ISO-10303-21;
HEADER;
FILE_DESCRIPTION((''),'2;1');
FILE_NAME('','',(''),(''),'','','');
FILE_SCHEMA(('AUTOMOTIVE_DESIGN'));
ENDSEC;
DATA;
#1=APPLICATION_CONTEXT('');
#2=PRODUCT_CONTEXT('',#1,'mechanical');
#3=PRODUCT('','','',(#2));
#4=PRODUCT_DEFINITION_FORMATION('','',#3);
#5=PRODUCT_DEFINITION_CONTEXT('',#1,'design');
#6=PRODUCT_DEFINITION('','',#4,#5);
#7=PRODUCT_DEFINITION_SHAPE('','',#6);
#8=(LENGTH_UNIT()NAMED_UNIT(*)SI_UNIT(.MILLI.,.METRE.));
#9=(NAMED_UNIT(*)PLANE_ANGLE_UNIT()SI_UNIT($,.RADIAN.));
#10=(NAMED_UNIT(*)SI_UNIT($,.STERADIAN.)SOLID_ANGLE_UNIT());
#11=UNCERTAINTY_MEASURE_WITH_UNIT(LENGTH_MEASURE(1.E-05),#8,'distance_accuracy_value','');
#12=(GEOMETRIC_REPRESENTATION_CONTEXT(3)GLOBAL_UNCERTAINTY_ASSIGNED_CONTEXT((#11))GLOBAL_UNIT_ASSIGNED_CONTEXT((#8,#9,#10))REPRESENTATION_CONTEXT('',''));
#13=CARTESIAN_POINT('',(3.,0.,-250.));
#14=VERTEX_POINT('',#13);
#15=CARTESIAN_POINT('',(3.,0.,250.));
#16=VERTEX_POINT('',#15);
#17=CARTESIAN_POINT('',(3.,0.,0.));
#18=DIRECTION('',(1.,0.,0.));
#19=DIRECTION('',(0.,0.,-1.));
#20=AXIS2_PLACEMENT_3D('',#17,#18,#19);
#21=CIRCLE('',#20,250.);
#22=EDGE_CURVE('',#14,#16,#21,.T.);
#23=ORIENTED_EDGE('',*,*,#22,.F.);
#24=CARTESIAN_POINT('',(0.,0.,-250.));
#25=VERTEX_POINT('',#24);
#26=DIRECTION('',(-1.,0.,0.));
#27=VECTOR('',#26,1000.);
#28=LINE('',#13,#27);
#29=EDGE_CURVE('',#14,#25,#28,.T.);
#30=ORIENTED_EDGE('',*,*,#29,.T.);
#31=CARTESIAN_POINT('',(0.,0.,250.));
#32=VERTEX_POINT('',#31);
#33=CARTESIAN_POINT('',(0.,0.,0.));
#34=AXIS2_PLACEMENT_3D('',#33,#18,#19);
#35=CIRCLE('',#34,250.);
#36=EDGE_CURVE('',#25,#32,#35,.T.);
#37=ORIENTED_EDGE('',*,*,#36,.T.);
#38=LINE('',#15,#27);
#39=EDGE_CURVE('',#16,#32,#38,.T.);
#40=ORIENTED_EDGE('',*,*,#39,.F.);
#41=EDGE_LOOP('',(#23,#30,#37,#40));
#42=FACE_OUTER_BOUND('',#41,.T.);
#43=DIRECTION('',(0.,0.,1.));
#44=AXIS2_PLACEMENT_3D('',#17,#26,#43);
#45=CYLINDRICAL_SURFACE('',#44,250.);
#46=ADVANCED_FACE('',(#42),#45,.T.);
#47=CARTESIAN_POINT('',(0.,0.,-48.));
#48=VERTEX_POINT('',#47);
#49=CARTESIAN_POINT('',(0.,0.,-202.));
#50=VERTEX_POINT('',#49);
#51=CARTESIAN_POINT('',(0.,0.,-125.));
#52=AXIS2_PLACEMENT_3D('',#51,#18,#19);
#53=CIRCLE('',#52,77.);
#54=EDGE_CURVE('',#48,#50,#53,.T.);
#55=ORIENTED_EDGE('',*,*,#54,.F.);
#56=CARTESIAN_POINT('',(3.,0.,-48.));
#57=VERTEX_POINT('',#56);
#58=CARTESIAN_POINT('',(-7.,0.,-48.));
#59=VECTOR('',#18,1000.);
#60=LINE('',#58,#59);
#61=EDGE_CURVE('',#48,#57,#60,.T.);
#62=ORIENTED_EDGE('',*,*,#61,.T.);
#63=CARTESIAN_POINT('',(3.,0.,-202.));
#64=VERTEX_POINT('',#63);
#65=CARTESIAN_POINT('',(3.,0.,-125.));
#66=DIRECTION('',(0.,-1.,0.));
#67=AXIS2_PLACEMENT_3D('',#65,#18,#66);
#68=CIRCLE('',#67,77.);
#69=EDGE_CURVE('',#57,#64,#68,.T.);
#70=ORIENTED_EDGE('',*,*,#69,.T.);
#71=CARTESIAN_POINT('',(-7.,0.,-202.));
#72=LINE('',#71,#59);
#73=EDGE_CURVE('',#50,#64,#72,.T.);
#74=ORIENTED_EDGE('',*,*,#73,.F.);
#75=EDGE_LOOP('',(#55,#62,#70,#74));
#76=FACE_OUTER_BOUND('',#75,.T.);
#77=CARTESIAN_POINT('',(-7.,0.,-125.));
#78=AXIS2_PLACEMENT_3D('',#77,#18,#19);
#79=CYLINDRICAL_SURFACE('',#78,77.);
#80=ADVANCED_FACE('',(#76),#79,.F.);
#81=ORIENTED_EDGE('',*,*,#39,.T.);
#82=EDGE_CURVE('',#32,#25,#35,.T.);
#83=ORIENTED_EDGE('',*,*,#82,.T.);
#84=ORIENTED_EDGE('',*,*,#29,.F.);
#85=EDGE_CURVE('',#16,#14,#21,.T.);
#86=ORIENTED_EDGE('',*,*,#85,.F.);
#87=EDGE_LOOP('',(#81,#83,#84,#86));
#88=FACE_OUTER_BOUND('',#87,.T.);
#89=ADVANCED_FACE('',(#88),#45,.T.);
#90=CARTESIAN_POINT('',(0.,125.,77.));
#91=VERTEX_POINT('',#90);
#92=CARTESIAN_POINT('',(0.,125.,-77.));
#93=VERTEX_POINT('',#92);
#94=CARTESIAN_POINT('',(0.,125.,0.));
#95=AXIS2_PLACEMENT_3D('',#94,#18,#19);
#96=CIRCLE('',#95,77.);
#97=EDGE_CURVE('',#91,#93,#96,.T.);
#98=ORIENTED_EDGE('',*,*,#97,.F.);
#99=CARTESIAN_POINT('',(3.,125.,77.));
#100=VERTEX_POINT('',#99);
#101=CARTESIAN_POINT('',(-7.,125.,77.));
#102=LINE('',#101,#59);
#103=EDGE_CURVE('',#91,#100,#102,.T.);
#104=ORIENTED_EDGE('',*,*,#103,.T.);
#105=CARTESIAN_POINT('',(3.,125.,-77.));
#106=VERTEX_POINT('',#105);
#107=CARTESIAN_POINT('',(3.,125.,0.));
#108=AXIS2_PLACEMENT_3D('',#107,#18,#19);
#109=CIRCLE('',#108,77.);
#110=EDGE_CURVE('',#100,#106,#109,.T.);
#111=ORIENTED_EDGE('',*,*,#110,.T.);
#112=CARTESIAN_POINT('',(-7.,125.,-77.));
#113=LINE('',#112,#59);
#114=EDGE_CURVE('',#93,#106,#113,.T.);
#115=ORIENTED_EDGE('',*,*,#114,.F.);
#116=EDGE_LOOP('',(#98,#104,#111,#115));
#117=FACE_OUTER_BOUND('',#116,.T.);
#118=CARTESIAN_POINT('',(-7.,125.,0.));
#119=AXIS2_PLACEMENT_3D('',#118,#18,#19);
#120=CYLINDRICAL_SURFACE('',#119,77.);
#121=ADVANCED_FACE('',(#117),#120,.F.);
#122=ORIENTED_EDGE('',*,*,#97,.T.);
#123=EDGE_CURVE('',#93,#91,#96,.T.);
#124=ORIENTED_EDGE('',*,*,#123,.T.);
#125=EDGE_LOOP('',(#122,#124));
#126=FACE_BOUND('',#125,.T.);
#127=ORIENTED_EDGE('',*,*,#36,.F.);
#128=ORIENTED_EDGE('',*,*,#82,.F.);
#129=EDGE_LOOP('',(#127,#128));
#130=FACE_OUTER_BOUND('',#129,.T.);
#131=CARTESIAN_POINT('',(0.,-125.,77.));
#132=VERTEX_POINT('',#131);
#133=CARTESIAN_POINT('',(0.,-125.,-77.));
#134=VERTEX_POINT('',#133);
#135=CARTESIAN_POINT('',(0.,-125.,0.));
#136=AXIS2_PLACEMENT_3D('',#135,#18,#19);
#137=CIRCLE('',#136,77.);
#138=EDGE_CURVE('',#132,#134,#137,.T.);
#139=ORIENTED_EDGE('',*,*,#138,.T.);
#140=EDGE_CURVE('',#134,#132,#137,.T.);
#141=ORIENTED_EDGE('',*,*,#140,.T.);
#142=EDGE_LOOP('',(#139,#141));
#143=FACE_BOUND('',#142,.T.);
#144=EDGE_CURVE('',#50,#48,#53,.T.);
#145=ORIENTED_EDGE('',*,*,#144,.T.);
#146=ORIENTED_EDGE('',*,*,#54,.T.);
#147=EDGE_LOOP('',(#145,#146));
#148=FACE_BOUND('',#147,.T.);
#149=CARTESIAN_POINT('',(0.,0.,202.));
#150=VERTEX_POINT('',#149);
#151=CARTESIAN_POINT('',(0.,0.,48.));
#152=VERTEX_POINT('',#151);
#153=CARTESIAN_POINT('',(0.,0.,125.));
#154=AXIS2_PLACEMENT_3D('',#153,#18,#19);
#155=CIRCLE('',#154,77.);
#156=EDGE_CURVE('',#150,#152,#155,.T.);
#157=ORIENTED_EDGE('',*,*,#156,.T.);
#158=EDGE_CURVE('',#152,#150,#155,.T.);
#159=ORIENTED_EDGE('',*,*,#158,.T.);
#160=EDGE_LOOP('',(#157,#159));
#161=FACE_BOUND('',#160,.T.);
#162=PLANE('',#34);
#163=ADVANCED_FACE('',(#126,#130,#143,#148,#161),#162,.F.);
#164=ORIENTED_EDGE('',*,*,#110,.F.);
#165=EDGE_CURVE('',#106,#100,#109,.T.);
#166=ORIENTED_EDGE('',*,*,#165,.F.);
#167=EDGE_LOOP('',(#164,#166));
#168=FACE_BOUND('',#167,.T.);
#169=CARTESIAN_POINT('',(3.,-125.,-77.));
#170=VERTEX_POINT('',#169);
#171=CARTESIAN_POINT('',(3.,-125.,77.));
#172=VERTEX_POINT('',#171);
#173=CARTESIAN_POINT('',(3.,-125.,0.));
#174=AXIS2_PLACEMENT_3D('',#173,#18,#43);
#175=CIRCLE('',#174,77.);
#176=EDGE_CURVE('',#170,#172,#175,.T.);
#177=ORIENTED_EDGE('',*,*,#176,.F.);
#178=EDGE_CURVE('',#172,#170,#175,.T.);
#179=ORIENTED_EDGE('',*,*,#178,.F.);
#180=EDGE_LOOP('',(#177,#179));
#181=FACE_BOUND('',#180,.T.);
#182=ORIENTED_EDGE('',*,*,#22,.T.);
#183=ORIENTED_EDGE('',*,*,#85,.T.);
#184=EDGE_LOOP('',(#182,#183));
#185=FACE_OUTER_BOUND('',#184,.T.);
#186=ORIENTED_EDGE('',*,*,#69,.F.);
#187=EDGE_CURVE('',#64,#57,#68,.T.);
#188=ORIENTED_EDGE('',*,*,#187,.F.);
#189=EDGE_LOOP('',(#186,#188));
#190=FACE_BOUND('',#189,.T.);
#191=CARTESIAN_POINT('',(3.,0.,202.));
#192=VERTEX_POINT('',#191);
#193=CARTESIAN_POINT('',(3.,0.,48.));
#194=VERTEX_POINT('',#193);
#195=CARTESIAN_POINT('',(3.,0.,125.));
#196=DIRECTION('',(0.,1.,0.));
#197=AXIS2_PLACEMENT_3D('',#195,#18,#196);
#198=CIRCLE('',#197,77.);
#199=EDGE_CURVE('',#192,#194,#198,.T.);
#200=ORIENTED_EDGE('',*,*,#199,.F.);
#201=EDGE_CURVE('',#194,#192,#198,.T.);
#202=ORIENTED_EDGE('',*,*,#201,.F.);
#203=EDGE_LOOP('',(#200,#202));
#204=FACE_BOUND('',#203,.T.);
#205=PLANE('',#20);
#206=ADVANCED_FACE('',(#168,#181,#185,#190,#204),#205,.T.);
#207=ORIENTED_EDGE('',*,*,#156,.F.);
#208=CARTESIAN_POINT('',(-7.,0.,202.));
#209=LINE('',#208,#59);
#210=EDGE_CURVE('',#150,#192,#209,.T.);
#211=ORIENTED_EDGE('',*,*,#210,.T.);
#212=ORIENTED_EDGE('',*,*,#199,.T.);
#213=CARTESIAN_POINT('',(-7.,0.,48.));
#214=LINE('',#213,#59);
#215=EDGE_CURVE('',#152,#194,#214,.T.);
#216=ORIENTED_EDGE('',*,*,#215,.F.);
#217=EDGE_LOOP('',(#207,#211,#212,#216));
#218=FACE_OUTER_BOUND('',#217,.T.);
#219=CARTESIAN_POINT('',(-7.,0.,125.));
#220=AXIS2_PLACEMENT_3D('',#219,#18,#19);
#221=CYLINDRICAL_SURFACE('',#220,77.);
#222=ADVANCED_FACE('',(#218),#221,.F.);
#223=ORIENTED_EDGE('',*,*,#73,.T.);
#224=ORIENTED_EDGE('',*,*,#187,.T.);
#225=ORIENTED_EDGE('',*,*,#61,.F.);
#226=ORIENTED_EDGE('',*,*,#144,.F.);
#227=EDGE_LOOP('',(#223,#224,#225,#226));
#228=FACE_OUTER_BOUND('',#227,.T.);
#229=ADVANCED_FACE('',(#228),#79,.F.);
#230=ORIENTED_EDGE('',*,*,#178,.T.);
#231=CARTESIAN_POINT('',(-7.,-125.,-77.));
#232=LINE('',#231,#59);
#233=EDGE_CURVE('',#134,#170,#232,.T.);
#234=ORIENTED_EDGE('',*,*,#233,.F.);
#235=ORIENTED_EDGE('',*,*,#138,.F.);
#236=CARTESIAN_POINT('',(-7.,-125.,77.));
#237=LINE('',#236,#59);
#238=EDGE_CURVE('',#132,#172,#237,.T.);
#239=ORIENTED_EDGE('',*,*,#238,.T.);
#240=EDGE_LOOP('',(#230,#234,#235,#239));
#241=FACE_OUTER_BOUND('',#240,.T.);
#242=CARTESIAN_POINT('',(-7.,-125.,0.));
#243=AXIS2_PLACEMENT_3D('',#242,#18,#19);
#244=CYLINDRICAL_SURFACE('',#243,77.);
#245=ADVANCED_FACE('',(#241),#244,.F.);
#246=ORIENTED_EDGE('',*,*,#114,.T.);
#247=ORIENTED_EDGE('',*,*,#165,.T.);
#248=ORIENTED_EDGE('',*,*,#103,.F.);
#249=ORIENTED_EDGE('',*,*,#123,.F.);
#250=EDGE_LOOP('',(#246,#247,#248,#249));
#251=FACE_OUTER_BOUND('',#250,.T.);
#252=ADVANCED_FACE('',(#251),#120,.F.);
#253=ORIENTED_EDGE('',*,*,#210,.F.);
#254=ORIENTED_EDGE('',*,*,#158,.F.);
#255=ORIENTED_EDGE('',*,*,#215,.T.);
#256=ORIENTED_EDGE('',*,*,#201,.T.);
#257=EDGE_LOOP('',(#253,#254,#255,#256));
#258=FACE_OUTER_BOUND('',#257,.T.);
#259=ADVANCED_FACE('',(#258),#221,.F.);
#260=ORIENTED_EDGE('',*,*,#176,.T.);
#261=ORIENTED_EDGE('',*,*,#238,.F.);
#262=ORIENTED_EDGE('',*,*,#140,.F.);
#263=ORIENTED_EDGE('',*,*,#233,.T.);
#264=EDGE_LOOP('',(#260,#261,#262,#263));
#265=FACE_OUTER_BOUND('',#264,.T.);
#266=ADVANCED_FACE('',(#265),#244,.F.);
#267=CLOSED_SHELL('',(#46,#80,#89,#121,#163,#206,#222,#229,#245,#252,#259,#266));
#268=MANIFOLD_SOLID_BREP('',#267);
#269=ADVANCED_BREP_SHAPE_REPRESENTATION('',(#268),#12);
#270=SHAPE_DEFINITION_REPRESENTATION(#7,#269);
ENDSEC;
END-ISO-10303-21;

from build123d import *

# Parameters (mm, degrees)
SKETCH1_R           = 250
BOSS_EXTRUDE1_DEPTH = 3
SKETCH2_R           = 77
CUT_EXTRUDE1_DEPTH  = 10
CIRPATTERN1_COUNT   = 4


with BuildPart() as part:
    # Sketch1 → Boss-Extrude1 (new body)
    with BuildSketch(Plane(origin=(0, 0, 0), x_dir=(0, 0, -1), z_dir=(1, 0, 0))):
        Circle(SKETCH1_R)
    extrude(amount=BOSS_EXTRUDE1_DEPTH)

    # Sketch2 → Cut-Extrude1 (cut)
    with BuildSketch(Plane(origin=(3, 0, 0), x_dir=(0, 0, -1), z_dir=(1, 0, 0))):
        with Locations((0, 125)):
            Circle(SKETCH2_R)
    cut_extrude1 = extrude(amount=-CUT_EXTRUDE1_DEPTH, mode=Mode.SUBTRACT)

    # CirPattern1: Cut-Extrude1 ×4 about axis
    cirpattern1_axis = Axis((0, 0, 0), (1, 0, 0))
    for i in range(1, CIRPATTERN1_COUNT):
        add(cut_extrude1.rotate(cirpattern1_axis, i * 360 / CIRPATTERN1_COUNT), mode=Mode.SUBTRACT)


solid = part.part
